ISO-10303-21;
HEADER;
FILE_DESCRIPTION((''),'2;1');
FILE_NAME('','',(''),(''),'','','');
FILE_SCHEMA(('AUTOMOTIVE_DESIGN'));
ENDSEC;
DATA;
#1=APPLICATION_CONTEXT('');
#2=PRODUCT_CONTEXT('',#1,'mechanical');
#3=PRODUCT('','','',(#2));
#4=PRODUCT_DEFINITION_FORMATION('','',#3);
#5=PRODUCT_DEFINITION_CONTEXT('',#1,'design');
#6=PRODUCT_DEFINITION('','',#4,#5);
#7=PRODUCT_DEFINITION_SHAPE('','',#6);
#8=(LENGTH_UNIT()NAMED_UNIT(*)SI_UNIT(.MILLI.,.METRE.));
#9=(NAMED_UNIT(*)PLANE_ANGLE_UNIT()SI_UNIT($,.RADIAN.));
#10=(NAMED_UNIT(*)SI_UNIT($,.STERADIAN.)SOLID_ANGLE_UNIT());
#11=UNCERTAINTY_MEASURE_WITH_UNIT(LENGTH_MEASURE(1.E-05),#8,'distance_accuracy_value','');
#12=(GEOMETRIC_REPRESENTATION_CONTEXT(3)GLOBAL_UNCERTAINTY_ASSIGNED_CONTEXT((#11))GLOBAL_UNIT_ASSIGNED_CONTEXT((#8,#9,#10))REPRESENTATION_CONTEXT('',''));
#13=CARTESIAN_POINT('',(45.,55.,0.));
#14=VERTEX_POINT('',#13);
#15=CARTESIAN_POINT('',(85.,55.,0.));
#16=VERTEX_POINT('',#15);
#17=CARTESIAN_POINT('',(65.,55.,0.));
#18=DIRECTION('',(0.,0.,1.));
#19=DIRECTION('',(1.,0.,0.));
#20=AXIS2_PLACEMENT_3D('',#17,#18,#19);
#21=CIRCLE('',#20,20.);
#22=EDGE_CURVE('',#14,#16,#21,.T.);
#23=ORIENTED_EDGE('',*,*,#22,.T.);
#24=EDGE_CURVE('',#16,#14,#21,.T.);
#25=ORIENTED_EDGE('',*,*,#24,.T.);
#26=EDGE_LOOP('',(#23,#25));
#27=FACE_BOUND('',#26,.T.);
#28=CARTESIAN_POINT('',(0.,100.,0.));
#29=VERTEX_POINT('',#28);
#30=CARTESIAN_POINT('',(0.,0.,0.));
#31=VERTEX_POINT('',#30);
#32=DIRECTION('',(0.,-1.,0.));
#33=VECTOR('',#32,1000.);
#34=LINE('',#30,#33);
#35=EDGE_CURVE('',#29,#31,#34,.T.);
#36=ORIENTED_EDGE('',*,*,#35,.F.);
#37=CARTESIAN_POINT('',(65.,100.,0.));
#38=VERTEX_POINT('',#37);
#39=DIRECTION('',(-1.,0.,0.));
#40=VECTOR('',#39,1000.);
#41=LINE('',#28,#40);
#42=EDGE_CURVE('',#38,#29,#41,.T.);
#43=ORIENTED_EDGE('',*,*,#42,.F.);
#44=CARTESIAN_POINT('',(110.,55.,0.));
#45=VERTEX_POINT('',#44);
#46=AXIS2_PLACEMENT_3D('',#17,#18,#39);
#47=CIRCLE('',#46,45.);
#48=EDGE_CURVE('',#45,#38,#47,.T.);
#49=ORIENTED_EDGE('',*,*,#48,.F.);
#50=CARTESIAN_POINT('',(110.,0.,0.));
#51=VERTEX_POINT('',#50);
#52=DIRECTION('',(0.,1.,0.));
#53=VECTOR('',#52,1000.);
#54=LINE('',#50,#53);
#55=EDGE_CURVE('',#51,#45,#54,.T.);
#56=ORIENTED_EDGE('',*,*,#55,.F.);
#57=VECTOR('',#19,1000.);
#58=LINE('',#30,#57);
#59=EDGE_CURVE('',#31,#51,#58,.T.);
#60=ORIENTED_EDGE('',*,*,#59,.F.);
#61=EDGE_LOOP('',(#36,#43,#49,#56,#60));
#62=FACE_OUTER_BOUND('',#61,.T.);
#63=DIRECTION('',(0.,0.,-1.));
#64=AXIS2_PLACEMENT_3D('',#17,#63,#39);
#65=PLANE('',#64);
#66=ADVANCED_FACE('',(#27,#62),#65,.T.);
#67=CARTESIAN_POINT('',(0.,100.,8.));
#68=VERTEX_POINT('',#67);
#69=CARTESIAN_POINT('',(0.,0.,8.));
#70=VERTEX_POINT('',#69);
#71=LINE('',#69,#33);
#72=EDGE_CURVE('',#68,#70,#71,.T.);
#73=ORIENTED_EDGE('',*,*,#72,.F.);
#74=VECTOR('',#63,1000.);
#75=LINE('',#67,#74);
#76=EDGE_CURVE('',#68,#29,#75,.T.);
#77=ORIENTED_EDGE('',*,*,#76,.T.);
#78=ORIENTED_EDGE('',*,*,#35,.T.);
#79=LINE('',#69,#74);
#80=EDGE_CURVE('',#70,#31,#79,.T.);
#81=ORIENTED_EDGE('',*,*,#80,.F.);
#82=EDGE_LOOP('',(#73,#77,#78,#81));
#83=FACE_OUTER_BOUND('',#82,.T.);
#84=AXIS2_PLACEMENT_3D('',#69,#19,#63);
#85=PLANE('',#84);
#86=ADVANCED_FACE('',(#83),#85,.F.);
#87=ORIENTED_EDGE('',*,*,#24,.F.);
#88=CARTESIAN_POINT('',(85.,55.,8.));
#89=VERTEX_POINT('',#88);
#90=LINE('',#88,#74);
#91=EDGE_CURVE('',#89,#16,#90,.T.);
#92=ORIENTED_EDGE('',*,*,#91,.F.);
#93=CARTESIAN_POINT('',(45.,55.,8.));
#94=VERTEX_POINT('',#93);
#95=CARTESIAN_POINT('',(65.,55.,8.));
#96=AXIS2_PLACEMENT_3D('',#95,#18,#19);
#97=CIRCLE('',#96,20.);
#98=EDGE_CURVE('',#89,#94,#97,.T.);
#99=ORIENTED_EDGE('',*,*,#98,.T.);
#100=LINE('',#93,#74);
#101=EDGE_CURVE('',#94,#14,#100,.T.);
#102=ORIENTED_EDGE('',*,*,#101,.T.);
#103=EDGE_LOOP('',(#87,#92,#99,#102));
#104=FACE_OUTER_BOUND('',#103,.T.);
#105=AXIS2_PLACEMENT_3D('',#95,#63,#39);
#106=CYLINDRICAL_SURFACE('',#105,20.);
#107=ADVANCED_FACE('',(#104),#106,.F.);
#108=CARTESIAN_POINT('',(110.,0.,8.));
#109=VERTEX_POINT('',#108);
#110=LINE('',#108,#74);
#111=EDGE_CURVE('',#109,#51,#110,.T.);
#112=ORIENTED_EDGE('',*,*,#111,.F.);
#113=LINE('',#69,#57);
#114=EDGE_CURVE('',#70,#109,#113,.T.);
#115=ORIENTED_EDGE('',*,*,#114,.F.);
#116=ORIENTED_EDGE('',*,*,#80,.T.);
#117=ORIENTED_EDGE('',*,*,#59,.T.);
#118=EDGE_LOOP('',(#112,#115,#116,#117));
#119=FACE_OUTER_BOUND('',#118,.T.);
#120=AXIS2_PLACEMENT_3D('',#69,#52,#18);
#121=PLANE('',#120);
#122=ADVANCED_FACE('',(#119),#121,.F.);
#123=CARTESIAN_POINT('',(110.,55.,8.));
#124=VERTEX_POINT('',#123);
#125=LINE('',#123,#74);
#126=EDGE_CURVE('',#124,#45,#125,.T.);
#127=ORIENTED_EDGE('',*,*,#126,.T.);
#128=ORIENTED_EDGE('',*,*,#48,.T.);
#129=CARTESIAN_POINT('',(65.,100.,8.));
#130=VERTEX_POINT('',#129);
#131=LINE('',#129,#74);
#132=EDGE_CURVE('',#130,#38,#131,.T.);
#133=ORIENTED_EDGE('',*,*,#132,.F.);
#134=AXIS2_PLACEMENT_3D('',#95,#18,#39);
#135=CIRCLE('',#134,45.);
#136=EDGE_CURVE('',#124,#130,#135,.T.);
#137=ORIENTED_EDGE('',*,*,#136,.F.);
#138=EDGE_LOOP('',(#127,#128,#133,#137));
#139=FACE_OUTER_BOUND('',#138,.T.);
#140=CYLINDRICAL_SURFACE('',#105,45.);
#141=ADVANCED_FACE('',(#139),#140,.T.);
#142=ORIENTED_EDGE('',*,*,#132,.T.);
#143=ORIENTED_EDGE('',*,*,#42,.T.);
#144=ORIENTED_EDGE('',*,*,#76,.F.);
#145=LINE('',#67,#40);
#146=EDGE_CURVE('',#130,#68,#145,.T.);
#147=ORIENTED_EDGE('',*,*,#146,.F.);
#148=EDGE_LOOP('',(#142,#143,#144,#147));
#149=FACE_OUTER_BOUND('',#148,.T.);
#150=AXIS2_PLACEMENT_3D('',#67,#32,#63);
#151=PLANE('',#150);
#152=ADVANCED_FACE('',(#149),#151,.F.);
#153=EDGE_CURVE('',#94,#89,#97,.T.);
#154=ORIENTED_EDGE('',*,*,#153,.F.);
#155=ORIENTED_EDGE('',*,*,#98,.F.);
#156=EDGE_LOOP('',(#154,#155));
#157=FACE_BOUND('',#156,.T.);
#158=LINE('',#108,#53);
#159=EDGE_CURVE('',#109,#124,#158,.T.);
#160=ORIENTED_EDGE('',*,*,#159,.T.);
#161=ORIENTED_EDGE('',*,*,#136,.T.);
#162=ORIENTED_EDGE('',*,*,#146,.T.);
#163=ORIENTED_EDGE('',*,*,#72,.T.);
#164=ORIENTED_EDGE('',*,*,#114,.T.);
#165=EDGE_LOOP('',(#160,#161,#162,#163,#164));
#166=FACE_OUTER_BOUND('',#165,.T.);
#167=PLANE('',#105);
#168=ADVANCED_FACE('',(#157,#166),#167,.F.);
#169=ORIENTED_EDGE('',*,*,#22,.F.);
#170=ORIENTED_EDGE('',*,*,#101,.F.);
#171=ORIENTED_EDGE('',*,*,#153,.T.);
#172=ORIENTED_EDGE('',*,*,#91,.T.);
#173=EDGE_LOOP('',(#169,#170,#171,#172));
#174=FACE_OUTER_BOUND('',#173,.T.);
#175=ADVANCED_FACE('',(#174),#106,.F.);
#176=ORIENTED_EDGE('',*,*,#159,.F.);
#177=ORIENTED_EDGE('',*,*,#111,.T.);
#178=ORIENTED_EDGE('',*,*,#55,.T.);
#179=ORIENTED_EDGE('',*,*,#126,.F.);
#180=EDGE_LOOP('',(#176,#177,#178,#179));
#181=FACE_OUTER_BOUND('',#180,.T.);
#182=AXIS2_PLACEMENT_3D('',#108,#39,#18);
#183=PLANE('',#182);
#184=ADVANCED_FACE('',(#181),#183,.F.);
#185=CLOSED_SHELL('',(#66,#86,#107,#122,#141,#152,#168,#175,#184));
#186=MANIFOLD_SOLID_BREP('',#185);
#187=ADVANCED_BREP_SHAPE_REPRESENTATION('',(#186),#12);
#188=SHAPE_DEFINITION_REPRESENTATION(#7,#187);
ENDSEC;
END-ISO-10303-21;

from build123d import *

# Parameters (mm, degrees)
SKETCH1_R           = 20
BOSS_EXTRUDE1_DEPTH = 8


with BuildPart() as part:
    # Sketch1 → Boss-Extrude1 (new body)
    with BuildSketch(Plane.XY):
        with BuildLine():
            Line((0, 0), (110, 0))
            Line((110, 0), (110, 55))
            ThreePointArc((110, 55), (96.819805153, 86.819805153), (65, 100))
            Line((65, 100), (0, 100))
            Line((0, 100), (0, 0))
        make_face()
        with Locations((65, 55)):
            Circle(SKETCH1_R, mode=Mode.SUBTRACT)
    extrude(amount=BOSS_EXTRUDE1_DEPTH)


solid = part.part
